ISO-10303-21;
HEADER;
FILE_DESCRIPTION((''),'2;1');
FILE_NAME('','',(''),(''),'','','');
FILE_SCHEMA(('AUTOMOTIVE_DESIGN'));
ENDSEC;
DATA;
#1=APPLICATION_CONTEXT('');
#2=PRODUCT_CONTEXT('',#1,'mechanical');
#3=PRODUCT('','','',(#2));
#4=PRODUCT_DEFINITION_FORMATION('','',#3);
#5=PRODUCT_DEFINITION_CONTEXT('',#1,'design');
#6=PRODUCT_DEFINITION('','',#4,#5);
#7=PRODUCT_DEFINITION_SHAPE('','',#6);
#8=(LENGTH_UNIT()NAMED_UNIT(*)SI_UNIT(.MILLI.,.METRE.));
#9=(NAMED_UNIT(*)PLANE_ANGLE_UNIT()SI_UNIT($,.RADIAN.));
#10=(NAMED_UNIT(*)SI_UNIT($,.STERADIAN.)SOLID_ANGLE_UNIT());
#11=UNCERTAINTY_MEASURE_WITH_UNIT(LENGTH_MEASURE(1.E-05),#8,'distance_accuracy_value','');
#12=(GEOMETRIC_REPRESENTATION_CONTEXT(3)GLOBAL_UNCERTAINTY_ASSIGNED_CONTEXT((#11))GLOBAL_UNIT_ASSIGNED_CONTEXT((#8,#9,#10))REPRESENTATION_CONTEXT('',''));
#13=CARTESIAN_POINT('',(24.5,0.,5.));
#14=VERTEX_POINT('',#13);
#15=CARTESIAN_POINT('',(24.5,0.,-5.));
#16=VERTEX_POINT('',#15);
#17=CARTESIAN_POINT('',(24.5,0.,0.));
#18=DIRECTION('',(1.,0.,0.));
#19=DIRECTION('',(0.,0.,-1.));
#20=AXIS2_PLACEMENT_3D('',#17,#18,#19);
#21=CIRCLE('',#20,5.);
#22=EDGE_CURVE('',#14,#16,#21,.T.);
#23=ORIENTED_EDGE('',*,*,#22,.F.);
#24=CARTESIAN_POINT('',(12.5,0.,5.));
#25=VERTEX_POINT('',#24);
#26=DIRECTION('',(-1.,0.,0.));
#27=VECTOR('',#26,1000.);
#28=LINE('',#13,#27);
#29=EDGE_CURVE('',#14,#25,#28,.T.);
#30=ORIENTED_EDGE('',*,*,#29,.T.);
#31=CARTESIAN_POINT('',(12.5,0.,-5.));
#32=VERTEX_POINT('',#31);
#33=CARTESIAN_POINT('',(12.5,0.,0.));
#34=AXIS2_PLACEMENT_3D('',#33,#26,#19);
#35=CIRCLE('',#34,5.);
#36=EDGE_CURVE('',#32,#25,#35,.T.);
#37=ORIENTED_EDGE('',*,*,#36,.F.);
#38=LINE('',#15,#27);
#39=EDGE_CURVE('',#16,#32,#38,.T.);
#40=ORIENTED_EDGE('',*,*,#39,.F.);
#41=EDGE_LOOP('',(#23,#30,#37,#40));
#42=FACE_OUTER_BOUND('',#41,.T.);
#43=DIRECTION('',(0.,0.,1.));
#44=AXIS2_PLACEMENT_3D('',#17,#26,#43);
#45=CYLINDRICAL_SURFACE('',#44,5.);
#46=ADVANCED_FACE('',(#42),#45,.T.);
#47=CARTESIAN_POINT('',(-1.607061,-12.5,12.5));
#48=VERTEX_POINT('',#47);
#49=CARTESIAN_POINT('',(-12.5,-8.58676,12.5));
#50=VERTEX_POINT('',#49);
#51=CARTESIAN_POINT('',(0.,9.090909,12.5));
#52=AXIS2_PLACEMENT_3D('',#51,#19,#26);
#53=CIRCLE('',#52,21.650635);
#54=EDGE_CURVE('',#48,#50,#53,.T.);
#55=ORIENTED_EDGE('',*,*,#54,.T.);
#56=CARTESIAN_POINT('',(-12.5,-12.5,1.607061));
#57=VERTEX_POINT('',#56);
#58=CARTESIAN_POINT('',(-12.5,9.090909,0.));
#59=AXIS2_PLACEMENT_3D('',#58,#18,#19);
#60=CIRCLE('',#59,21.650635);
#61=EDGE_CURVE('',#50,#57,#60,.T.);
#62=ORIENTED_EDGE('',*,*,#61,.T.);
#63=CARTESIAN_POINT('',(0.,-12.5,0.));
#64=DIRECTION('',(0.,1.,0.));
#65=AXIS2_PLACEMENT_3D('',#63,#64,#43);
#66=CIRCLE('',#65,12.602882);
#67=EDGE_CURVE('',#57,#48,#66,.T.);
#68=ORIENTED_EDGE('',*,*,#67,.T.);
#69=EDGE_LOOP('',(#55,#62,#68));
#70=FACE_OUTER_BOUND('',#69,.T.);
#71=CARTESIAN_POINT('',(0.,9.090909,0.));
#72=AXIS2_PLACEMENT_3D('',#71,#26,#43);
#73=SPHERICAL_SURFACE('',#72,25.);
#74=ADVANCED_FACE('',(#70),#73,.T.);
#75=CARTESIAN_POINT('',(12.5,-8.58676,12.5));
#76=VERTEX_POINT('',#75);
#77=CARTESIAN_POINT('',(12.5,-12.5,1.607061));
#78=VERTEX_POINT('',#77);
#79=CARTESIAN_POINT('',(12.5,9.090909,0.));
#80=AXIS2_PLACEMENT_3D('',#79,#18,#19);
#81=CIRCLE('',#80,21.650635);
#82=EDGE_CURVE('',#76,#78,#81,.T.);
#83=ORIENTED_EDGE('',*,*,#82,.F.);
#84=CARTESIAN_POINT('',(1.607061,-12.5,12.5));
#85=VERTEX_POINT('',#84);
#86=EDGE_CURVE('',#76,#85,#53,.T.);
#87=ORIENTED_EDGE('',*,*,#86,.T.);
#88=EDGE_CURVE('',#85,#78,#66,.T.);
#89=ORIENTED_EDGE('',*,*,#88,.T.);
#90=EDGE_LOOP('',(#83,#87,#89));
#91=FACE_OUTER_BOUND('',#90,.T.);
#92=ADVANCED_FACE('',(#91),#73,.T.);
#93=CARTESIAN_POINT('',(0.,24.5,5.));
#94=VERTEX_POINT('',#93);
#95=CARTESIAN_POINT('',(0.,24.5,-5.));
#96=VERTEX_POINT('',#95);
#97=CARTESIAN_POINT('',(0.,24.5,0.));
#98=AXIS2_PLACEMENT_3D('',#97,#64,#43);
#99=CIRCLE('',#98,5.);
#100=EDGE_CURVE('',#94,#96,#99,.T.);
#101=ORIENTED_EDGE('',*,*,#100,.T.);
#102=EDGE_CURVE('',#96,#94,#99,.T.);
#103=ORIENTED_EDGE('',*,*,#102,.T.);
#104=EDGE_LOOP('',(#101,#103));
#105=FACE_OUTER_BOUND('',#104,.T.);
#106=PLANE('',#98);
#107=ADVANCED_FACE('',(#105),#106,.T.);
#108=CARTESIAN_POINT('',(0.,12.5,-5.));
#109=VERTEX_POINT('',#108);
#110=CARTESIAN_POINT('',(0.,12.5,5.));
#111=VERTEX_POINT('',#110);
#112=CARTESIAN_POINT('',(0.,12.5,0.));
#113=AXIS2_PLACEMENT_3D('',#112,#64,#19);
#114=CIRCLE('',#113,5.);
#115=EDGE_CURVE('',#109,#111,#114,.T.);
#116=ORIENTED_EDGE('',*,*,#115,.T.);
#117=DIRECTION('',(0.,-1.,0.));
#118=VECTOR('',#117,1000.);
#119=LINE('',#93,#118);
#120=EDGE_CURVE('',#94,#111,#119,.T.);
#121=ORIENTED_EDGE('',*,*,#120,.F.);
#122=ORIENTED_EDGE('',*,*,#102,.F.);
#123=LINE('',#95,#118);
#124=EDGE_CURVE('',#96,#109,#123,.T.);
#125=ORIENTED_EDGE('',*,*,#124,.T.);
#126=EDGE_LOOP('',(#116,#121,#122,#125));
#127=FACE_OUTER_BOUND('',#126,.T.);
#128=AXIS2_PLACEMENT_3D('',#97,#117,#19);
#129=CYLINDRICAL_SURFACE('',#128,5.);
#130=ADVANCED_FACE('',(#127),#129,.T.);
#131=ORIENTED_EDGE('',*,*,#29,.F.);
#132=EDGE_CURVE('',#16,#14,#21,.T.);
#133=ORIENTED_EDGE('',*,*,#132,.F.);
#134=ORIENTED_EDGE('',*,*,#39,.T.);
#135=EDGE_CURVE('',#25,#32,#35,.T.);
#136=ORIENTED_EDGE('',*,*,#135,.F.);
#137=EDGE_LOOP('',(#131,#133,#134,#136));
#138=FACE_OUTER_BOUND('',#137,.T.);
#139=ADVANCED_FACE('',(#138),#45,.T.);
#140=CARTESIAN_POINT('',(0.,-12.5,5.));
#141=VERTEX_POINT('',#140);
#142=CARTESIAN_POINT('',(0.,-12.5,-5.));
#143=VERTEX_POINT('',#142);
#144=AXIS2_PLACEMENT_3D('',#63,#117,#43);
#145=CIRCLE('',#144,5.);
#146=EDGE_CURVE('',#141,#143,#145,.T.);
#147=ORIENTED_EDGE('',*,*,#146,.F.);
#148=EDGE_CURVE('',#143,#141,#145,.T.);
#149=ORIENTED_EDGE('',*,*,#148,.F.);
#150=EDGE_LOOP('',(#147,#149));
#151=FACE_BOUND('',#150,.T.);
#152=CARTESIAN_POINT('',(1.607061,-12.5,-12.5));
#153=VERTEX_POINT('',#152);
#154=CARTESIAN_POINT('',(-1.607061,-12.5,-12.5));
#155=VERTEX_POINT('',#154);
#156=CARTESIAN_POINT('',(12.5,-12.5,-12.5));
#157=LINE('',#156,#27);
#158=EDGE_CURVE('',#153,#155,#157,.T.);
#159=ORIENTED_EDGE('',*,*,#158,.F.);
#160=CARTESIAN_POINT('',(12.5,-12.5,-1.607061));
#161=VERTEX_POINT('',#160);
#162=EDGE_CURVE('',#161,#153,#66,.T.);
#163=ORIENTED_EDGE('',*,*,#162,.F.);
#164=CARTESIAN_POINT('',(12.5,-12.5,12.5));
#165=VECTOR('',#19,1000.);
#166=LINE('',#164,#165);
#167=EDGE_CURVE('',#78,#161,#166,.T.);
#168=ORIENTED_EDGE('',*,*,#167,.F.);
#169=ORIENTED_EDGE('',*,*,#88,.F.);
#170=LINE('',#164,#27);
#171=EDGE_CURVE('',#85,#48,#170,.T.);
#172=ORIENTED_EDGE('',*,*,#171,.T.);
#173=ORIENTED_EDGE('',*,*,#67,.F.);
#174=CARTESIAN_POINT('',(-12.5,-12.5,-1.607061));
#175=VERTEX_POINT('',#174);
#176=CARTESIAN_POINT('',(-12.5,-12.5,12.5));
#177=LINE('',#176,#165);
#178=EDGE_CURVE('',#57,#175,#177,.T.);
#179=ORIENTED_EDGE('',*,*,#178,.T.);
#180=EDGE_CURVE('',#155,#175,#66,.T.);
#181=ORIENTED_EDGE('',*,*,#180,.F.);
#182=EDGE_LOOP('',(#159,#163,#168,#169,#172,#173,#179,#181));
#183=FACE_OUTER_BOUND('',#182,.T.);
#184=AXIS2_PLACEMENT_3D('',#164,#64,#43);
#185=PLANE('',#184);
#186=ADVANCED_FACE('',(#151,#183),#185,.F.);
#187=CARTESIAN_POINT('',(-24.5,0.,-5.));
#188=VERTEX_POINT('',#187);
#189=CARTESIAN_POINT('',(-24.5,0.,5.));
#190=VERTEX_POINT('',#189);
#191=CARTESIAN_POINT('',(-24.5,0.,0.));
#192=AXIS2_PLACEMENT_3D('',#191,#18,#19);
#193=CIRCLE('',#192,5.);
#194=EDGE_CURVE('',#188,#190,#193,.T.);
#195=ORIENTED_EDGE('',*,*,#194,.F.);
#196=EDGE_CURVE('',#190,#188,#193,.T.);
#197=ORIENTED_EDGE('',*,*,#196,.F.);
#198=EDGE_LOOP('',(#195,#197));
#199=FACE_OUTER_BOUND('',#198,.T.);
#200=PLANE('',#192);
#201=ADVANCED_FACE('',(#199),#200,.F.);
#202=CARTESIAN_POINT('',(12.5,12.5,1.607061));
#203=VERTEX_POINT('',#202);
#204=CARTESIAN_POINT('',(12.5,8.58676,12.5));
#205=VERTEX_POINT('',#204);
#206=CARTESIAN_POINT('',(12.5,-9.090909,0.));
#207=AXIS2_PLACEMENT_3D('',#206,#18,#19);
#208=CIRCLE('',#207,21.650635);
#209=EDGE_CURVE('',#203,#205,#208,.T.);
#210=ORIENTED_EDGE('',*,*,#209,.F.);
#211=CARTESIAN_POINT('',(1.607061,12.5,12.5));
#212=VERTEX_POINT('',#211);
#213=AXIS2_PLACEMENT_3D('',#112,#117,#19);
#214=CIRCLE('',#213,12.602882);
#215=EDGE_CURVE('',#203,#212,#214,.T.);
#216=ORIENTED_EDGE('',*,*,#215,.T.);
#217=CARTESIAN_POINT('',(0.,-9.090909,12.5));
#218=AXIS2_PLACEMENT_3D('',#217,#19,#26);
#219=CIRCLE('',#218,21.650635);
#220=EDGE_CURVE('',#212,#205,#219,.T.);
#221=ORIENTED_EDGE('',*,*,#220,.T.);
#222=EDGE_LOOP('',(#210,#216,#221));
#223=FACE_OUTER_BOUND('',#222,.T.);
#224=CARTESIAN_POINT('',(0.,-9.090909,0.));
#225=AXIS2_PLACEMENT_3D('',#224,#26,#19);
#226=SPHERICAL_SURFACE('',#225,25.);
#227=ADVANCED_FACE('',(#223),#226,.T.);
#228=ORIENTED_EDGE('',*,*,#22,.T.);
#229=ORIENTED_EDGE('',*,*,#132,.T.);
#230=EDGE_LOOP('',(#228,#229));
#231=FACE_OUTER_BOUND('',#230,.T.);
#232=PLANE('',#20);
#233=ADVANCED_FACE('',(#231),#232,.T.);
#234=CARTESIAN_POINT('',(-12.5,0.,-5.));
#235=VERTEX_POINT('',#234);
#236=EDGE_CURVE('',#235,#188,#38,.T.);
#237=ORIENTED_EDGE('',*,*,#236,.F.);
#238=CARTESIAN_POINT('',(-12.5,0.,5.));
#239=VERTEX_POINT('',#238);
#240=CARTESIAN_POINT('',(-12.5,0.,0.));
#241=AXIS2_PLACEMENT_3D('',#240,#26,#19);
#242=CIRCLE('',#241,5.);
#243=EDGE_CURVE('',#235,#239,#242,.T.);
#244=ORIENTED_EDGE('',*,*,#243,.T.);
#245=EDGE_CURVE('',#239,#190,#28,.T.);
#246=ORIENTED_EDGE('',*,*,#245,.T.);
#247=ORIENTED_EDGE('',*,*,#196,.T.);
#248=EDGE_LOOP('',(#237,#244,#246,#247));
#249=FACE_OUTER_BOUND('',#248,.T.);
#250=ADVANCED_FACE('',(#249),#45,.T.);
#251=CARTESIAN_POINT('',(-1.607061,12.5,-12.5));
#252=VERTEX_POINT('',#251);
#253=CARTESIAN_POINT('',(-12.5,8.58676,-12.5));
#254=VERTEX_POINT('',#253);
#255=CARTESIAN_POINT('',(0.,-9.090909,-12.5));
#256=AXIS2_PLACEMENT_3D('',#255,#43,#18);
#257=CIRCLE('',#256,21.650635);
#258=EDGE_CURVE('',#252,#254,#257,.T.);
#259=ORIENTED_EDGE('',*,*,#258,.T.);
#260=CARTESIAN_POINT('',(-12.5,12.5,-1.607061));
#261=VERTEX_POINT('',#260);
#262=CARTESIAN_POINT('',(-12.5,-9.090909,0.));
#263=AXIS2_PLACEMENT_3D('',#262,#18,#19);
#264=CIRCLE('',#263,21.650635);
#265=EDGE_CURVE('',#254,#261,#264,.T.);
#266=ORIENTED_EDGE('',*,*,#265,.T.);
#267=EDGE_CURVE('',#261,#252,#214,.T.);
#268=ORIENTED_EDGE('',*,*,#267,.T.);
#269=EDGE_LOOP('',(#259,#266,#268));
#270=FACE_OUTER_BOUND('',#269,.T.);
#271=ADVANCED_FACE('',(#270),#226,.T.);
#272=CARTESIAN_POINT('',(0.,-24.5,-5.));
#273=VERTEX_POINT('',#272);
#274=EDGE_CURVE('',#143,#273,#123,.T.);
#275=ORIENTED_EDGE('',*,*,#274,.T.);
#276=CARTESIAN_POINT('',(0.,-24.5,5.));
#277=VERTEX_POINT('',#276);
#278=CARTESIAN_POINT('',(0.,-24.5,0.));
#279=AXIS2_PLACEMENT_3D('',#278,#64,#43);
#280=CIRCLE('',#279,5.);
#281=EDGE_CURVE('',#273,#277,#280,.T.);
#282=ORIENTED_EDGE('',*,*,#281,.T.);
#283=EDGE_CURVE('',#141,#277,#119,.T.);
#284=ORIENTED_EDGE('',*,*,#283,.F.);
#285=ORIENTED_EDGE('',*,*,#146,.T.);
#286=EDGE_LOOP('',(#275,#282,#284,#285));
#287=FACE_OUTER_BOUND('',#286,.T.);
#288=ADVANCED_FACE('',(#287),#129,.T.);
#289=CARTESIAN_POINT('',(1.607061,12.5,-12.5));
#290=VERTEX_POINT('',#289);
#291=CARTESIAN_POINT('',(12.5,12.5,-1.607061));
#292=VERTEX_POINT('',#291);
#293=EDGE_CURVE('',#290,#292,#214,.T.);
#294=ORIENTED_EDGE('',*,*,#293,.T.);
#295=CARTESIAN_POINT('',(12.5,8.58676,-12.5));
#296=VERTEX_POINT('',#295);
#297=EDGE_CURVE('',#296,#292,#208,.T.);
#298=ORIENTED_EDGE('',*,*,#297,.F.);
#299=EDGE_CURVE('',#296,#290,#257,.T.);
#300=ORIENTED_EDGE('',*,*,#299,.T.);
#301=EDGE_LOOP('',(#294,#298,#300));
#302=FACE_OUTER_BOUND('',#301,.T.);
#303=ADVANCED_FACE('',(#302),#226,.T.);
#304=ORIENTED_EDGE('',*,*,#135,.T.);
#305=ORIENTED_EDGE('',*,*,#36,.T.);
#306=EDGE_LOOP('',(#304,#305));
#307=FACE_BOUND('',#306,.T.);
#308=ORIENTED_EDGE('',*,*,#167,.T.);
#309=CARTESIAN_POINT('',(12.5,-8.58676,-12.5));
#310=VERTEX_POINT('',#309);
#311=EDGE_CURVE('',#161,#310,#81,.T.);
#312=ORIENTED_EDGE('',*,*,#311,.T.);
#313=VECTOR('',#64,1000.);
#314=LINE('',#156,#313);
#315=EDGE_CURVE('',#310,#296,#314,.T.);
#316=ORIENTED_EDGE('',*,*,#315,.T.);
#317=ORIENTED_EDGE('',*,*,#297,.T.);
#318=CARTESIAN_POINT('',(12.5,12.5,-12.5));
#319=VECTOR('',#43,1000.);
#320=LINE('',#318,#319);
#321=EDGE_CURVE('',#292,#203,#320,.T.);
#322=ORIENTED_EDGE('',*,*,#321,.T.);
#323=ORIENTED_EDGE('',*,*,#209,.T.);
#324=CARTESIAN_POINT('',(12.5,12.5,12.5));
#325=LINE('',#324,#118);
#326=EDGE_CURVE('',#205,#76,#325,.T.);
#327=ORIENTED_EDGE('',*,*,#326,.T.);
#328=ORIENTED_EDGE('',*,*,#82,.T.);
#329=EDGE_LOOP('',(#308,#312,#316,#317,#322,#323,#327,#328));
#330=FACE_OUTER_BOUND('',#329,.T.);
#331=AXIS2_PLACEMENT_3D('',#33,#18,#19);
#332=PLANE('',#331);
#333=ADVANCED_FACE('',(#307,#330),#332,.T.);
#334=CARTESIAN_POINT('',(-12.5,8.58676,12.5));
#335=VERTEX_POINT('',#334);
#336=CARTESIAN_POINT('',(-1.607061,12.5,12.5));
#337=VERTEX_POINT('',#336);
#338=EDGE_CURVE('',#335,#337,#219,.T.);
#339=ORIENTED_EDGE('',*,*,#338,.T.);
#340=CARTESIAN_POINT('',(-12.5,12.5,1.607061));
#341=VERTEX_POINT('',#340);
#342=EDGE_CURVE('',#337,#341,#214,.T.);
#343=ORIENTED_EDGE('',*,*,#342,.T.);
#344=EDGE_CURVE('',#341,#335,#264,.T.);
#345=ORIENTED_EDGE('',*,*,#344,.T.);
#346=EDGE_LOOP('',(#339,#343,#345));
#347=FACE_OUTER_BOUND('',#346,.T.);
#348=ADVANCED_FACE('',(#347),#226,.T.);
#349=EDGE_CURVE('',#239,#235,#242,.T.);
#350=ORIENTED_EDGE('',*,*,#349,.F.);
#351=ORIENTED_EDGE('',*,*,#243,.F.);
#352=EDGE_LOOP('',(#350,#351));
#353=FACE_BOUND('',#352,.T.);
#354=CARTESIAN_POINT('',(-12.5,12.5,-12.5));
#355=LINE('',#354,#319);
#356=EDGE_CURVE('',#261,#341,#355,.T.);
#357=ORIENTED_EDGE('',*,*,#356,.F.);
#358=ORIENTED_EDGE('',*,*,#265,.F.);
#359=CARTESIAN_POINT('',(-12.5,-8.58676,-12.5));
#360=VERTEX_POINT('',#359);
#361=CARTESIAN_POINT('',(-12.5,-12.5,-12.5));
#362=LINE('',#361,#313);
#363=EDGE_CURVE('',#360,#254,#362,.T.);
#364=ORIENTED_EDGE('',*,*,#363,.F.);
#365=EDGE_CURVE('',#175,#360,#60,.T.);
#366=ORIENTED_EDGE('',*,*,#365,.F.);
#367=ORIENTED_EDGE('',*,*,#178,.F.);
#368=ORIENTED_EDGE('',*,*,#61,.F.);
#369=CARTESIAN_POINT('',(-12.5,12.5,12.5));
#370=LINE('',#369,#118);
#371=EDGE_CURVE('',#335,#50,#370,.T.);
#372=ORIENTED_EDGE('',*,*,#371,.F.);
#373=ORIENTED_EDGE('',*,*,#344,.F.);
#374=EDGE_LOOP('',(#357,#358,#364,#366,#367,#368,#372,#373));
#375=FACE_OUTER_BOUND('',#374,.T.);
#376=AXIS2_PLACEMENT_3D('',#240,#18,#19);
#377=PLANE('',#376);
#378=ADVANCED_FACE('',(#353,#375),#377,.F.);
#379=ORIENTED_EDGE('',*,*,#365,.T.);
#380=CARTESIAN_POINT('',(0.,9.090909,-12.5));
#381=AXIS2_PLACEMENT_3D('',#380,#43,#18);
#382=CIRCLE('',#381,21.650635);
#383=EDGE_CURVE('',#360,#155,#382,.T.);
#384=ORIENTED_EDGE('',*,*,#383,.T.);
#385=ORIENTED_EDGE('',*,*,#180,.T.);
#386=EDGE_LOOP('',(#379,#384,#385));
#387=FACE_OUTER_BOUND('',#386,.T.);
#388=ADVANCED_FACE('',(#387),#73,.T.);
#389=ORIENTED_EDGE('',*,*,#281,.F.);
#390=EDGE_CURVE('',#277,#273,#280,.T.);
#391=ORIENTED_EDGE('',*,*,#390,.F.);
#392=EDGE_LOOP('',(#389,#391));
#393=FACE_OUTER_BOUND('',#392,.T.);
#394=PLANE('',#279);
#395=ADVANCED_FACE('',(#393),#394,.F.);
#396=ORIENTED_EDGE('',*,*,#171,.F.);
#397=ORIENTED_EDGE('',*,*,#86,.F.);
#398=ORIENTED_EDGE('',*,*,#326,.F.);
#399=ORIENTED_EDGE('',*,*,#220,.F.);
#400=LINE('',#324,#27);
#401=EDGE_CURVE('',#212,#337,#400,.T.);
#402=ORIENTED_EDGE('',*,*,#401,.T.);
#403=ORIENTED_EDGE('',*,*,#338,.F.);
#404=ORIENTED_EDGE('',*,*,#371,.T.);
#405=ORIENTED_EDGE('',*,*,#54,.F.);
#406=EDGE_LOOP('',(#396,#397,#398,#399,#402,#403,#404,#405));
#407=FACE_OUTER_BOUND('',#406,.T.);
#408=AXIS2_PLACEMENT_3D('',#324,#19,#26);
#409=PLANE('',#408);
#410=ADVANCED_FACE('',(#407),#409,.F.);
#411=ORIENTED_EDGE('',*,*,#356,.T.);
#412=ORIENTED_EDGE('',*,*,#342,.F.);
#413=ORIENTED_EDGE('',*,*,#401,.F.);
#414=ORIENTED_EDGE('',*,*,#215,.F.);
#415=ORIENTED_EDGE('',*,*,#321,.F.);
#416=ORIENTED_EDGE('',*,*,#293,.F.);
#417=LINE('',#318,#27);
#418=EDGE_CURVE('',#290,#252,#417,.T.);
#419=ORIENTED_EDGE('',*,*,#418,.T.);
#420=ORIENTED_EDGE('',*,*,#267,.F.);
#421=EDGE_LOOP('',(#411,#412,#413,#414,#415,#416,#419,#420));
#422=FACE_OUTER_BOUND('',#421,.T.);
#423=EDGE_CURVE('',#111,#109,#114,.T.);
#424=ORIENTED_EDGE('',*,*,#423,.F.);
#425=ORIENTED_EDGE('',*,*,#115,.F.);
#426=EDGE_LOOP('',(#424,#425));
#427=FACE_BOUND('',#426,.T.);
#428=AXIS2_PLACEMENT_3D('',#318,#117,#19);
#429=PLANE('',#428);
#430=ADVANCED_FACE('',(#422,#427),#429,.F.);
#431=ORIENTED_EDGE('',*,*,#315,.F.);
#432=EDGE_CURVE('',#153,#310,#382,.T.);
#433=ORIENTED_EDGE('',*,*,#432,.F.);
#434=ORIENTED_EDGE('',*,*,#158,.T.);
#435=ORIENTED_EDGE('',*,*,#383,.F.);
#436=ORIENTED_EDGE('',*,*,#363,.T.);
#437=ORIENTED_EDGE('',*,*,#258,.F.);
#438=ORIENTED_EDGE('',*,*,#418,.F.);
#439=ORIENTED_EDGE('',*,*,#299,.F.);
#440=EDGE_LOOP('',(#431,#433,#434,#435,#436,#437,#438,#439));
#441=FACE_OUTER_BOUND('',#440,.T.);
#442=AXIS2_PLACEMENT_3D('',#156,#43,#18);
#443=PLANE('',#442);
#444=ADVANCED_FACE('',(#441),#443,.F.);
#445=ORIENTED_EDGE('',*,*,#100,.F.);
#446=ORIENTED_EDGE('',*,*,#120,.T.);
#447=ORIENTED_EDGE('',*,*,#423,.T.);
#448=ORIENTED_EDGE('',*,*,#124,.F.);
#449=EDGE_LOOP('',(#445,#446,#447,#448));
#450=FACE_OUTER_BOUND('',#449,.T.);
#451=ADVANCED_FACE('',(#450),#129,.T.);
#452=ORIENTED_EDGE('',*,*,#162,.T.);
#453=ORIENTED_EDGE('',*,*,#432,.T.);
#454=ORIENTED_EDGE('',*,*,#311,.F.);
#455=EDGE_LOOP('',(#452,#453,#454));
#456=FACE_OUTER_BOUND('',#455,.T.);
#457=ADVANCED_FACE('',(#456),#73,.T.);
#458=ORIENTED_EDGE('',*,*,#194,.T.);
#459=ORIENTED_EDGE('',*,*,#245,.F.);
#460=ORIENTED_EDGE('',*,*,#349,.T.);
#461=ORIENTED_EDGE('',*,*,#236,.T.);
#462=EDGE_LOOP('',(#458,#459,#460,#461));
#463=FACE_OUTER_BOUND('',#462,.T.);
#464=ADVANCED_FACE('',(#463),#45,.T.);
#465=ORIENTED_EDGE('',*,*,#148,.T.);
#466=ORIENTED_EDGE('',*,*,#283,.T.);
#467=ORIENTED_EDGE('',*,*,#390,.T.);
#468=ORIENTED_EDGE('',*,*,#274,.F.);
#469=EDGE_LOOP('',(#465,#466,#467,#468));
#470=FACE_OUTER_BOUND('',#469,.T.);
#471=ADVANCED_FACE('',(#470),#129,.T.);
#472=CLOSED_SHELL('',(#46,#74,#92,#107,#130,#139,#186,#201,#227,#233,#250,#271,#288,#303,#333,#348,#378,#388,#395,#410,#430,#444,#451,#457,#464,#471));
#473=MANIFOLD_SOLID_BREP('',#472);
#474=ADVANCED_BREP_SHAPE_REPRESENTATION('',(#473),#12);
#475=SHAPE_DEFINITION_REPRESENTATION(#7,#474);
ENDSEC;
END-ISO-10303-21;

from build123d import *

# Parameters (mm, degrees)
EXTRUDE_1_DEPTH      = 12.5
EXTRUDE_1_DEPTH_BACK = 12.5
SKETCH_1_W           = 25
SKETCH_1_H           = 25
EXTRUDE_2_DEPTH      = 24.5
EXTRUDE_2_DEPTH_BACK = 24.5
SKETCH_4_R           = 5
EXTRUDE_3_DEPTH      = 24.5
EXTRUDE_3_DEPTH_BACK = 24.5
SKETCH_5_R           = 5


with BuildPart() as part:
    # 草图1 → 凸台-拉伸1 (new, two sides: drawn at the far end of the back side and taken through both)
    with BuildSketch(Plane(origin=(0, 0, 0), x_dir=(0, 0, -1), z_dir=(1, 0, 0)).offset(-EXTRUDE_1_DEPTH_BACK)):
        Rectangle(SKETCH_1_W, SKETCH_1_H)
    extrude(amount=EXTRUDE_1_DEPTH + EXTRUDE_1_DEPTH_BACK)

    # 草图2 → 切除-旋转1 (revolve, cut)
    with BuildSketch(Plane(origin=(0, 0, 0), x_dir=(0, 0, -1), z_dir=(1, 0, 0))):
        with BuildLine():
            Line((0, -25), (-25, -25))
            Line((-25, -25), (-25, 9.090909091))
            ThreePointArc((-25, 9.090909091), (-17.67766953, -8.586760439), (0, -15.909090909))
            Line((0, -15.909090909), (0, -25))
        make_face()
    revolve(axis=Axis((0, -15.909090909, 0), (0, -1, 0)), mode=Mode.SUBTRACT)

    # 草图3 → 切除-旋转2 (revolve, cut)
    with BuildSketch(Plane(origin=(0, 0, 0), x_dir=(0, 0, -1), z_dir=(1, 0, 0))):
        with BuildLine():
            Line((0, 25), (25, 25))
            Line((25, 25), (25, -9.090909091))
            ThreePointArc((25, -9.090909091), (17.67766953, 8.586760439), (0, 15.909090909))
            Line((0, 15.909090909), (0, 25))
        make_face()
    revolve(axis=Axis((0, 15.909090909, 0), (0, 1, 0)), mode=Mode.SUBTRACT)

    # 草图4 → 凸台-拉伸2 (add, two sides: drawn at the far end of the back side and taken through both)
    with BuildSketch(Plane(origin=(0, 0, 0), x_dir=(1, 0, 0), z_dir=(0, 1, 0)).offset(-EXTRUDE_2_DEPTH_BACK)):
        with Locations(Location((0, 0, 0), (0, 0, 270))):
            Circle(SKETCH_4_R)
    extrude(amount=EXTRUDE_2_DEPTH + EXTRUDE_2_DEPTH_BACK)

    # 草图5 → 凸台-拉伸3 (add, two sides: drawn at the far end of the back side and taken through both)
    with BuildSketch(Plane(origin=(0, 0, 0), x_dir=(0, 0, -1), z_dir=(1, 0, 0)).offset(-EXTRUDE_3_DEPTH_BACK)):
        Circle(SKETCH_5_R)
    extrude(amount=EXTRUDE_3_DEPTH + EXTRUDE_3_DEPTH_BACK)


solid = part.part
